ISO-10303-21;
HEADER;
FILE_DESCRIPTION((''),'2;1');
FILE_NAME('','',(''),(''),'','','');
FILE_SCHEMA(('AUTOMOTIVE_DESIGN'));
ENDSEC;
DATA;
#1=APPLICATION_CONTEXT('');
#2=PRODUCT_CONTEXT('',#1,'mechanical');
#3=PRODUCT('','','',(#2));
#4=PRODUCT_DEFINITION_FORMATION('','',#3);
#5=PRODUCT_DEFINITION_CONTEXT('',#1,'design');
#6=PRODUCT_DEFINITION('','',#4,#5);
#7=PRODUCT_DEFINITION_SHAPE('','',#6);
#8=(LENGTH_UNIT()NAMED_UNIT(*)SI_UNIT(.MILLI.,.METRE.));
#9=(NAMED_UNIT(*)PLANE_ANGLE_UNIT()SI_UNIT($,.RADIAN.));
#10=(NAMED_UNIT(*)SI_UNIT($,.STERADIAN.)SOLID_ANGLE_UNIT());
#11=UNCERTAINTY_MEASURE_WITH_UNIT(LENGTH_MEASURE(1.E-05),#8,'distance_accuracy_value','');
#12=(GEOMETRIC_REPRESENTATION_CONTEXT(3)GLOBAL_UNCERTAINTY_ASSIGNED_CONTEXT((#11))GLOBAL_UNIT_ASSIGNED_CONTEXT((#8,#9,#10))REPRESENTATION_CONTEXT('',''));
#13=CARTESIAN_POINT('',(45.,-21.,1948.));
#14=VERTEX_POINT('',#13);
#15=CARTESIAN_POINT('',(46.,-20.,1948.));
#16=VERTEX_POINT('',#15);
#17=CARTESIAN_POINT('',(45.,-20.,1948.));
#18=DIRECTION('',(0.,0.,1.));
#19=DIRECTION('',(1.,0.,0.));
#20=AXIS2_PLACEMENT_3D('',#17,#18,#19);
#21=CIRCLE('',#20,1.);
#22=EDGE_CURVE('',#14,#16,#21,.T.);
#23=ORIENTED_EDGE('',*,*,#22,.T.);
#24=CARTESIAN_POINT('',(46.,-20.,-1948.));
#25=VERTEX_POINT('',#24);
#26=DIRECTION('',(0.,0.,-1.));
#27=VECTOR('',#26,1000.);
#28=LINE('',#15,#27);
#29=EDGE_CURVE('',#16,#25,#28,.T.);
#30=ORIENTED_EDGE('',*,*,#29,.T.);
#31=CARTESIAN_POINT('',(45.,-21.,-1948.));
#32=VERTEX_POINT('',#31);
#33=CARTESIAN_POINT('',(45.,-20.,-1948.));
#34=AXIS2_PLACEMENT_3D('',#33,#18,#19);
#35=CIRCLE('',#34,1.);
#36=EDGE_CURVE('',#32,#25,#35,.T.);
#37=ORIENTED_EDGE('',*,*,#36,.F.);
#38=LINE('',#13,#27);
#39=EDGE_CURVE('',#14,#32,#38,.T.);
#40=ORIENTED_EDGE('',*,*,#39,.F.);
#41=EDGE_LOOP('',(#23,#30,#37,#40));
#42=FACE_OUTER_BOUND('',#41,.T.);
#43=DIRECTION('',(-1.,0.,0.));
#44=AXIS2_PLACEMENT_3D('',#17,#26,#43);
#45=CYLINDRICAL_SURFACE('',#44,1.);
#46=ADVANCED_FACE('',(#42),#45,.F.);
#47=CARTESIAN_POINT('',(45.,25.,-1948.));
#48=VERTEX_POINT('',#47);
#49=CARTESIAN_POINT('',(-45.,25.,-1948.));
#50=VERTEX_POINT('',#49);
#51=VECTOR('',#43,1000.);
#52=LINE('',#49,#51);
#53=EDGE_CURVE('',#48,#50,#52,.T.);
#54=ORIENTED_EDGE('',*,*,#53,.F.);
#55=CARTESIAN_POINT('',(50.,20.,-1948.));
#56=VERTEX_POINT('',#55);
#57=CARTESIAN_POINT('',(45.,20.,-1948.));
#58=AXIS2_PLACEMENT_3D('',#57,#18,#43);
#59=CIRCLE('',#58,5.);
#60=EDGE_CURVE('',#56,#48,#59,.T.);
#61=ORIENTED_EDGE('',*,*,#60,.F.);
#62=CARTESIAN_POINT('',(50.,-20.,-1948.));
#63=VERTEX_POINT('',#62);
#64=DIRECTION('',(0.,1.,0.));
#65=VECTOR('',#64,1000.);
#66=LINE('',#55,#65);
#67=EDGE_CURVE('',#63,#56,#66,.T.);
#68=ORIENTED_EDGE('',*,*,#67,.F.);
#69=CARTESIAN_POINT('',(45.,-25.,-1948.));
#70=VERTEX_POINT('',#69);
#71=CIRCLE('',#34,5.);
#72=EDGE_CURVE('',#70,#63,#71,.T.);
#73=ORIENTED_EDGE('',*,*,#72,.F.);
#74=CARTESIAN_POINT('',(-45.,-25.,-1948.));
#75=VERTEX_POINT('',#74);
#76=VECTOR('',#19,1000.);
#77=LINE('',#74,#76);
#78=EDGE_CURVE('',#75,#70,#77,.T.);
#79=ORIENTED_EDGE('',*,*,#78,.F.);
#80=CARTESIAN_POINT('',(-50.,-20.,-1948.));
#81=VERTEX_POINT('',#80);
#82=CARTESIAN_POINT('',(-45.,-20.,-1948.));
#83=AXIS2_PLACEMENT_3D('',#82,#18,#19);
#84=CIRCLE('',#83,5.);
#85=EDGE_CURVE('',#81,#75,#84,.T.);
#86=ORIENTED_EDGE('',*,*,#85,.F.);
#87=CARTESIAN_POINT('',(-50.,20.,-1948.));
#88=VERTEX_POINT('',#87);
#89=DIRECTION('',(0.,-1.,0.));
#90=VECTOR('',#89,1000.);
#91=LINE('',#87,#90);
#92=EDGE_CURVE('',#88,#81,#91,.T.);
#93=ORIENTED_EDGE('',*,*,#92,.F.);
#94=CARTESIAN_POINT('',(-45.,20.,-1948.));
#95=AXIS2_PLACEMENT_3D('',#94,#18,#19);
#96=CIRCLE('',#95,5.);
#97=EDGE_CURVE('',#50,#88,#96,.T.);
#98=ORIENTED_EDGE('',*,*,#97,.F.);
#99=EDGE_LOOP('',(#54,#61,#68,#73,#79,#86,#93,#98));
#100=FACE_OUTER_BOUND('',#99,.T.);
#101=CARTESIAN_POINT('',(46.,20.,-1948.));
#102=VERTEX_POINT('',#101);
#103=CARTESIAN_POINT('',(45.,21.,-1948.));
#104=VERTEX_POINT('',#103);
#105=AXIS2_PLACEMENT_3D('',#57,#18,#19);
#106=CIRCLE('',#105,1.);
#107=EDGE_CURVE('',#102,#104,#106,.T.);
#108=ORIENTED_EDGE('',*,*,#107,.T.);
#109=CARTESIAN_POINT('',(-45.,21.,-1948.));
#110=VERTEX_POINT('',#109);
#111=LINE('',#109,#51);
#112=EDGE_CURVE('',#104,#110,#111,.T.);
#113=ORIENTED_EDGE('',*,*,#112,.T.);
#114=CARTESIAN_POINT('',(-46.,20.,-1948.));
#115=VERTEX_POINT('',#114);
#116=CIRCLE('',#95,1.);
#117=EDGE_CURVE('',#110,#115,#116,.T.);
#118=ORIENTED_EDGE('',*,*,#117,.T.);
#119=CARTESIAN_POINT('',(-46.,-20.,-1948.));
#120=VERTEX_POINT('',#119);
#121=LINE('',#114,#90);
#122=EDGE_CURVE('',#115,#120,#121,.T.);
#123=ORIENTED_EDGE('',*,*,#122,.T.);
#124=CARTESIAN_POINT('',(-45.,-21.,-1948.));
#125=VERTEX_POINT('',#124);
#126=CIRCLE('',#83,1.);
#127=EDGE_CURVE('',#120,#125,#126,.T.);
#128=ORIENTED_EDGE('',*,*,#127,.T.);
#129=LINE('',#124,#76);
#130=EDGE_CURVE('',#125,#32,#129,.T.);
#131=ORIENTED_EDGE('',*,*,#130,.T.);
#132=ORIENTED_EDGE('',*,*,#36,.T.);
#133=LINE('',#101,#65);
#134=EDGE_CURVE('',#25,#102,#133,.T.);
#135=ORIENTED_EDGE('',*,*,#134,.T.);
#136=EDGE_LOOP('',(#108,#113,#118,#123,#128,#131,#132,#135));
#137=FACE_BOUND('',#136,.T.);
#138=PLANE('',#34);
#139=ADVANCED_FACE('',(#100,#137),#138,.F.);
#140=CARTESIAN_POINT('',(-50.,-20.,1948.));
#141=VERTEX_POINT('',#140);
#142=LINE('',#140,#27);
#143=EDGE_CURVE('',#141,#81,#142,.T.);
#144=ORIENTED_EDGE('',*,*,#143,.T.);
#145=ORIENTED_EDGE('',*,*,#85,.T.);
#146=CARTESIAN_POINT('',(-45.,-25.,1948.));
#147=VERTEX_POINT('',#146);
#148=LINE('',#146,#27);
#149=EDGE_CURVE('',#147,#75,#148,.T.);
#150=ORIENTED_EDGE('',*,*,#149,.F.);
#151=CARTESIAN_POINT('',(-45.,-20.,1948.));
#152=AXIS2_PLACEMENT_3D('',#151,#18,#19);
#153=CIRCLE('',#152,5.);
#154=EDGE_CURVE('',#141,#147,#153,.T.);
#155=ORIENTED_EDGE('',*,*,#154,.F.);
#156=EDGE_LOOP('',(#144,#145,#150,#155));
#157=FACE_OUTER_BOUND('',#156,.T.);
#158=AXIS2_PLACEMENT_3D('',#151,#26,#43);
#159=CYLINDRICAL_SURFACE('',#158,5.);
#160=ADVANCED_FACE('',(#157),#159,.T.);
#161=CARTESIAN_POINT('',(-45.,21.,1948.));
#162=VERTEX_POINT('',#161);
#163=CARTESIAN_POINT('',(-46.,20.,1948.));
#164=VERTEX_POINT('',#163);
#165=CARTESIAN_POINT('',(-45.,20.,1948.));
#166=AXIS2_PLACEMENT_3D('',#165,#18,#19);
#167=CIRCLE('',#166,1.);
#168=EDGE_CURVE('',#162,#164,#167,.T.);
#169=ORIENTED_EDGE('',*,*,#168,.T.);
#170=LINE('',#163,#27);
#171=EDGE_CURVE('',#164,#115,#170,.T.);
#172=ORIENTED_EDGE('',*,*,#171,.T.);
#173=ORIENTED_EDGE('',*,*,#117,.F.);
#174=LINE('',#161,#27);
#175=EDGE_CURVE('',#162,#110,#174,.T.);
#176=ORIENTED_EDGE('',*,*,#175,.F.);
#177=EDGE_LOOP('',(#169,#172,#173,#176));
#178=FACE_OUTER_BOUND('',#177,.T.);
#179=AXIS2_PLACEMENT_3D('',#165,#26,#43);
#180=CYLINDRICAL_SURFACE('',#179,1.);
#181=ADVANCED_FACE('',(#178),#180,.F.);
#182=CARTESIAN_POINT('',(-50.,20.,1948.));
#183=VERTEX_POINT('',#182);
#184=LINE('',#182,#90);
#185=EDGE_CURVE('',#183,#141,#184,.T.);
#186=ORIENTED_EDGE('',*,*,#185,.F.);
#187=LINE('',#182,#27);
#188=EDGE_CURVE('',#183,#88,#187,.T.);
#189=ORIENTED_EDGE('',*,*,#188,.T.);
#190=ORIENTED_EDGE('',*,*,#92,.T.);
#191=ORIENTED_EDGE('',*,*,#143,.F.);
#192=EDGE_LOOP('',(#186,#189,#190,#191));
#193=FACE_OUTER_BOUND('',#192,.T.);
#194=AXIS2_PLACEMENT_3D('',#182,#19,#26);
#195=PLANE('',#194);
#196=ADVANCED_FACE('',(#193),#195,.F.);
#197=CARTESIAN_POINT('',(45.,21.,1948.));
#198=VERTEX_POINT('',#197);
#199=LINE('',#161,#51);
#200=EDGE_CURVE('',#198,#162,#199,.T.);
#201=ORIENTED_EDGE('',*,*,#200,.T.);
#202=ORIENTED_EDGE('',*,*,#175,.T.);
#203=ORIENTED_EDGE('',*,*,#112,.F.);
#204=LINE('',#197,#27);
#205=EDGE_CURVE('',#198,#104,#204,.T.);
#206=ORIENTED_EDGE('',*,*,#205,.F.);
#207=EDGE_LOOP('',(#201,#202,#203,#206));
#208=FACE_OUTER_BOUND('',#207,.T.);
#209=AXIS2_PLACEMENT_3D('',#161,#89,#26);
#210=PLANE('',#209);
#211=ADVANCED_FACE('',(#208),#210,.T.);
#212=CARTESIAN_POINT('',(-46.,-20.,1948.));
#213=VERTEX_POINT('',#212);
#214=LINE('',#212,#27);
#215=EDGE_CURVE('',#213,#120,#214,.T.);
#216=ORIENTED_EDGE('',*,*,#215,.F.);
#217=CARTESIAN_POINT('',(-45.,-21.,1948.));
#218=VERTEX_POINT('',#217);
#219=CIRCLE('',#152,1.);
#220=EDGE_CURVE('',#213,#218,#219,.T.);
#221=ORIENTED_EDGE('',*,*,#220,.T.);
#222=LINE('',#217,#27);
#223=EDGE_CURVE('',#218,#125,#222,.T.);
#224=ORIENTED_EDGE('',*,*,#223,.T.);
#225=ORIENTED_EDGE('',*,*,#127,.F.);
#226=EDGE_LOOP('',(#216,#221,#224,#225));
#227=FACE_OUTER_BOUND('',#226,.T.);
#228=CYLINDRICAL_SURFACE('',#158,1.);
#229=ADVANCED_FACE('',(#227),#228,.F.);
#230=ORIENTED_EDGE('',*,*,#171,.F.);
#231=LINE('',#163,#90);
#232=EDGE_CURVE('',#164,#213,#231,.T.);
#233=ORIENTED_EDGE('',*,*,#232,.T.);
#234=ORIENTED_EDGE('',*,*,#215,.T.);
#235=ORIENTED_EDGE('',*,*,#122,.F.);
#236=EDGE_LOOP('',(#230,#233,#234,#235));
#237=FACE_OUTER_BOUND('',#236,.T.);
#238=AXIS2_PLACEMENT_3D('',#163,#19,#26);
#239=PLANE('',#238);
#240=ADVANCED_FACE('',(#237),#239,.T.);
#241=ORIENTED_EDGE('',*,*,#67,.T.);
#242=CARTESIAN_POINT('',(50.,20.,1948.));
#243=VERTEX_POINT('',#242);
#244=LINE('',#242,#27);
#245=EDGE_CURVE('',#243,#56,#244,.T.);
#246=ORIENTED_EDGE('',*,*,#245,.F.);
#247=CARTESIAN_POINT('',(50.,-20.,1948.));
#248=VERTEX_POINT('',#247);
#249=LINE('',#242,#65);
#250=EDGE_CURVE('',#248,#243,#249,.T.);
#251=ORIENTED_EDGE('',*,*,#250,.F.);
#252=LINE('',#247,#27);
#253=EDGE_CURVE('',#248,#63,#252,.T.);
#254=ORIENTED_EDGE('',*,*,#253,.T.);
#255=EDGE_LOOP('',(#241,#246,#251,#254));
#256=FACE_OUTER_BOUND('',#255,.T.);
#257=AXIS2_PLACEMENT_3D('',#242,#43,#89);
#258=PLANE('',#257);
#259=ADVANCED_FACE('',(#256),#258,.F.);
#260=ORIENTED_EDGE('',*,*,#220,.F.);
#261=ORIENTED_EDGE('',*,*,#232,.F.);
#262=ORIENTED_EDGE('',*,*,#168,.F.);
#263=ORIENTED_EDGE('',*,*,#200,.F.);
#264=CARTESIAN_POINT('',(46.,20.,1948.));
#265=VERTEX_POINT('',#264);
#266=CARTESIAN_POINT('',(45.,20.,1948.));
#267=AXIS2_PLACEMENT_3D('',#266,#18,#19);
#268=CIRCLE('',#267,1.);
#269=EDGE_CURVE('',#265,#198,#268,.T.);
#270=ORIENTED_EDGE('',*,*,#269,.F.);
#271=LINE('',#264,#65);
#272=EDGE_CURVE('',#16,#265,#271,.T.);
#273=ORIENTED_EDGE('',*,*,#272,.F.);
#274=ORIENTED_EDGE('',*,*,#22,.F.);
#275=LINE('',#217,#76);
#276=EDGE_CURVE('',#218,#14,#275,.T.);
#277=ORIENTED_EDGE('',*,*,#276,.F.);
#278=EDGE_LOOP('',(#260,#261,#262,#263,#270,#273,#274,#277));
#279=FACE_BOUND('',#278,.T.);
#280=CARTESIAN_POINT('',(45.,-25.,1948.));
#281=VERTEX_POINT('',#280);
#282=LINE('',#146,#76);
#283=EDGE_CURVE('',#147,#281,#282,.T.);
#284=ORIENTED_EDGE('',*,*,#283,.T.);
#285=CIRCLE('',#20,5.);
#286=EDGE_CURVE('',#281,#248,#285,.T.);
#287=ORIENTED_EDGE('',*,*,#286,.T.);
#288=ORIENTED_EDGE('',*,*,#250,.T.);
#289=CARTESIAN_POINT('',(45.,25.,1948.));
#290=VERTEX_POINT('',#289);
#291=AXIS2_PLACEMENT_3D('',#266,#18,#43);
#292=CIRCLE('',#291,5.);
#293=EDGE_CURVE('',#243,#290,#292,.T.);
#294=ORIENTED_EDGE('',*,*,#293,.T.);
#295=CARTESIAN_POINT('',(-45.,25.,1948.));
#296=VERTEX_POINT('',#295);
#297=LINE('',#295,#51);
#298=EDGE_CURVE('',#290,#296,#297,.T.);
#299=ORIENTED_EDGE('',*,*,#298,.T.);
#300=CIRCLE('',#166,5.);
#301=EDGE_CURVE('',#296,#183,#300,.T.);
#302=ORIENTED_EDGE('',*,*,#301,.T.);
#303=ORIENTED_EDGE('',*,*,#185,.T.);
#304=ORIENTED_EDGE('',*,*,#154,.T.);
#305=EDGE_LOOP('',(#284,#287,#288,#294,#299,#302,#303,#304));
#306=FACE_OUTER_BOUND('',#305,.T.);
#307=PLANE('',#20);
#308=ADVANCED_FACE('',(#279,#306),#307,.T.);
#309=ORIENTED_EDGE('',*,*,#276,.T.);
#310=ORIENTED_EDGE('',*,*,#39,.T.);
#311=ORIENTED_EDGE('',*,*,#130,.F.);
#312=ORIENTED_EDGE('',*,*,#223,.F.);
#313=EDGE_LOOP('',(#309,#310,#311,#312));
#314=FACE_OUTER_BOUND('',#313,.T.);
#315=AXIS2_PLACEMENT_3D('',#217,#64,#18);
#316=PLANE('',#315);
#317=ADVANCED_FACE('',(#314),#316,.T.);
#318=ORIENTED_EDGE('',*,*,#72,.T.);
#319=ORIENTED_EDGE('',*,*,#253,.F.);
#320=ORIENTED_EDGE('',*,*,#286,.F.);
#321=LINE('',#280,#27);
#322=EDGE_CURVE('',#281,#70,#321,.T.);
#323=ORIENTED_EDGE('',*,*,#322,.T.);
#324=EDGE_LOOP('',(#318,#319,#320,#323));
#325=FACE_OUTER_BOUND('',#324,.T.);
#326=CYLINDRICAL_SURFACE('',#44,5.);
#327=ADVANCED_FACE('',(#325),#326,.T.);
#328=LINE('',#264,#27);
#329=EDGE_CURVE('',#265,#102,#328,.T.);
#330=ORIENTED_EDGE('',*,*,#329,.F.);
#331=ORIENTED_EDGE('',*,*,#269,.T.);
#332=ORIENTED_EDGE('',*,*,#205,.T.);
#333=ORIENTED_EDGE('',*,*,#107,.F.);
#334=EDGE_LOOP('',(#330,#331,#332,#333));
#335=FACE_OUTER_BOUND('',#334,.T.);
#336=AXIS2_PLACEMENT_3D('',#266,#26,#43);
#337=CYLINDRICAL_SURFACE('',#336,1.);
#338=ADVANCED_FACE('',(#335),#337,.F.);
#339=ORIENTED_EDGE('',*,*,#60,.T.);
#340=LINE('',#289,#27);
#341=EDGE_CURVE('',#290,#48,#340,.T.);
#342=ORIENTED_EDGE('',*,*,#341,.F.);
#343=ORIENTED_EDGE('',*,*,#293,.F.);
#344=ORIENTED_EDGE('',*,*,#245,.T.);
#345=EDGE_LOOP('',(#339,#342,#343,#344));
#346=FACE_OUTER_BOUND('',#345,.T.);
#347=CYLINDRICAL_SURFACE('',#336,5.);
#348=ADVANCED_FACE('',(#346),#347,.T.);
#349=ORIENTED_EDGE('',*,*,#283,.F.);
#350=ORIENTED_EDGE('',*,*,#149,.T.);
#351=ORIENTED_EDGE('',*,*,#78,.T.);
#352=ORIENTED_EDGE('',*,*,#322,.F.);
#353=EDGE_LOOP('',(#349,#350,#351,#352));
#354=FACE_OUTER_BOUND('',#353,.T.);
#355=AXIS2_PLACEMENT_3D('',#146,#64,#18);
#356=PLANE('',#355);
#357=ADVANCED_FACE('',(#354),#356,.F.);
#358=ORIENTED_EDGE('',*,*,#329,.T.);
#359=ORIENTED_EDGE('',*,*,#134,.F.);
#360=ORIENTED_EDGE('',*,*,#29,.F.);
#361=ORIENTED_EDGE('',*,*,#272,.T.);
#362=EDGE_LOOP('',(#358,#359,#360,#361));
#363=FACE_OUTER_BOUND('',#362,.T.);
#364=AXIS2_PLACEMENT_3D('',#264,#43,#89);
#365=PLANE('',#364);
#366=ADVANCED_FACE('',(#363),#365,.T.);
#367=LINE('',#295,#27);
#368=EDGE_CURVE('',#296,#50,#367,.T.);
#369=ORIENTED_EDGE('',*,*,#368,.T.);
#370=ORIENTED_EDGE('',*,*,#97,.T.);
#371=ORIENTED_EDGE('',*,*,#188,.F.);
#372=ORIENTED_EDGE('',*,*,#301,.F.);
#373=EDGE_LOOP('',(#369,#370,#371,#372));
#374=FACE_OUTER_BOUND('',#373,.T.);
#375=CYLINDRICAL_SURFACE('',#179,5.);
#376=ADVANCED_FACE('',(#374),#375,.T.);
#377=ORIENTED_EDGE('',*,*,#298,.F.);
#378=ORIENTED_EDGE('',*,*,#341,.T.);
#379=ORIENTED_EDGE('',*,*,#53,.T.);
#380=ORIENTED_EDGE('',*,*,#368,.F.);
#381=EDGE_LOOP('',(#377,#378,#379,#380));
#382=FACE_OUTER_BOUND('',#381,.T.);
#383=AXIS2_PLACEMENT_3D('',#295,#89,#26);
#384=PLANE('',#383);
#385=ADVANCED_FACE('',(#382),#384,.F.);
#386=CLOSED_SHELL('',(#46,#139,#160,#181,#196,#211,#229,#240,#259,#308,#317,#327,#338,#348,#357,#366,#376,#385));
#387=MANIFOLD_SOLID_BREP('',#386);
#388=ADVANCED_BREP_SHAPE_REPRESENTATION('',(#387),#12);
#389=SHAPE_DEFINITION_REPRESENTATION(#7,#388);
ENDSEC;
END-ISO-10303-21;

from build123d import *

# Parameters (mm, degrees)
EXTRUDE_1_DEPTH = 1948


with BuildPart() as part:
    # 草图1 → 拉伸-薄壁1 (new, symmetric)
    with BuildSketch(Plane.XY):
        with BuildLine():
            Line((-45, 25), (45, 25))
            ThreePointArc((45, 25), (48.535533906, 23.535533906), (50, 20))
            Line((50, 20), (50, -20))
            ThreePointArc((50, -20), (48.535533906, -23.535533906), (45, -25))
            Line((45, -25), (-45, -25))
            ThreePointArc((-45, -25), (-48.535533906, -23.535533906), (-50, -20))
            Line((-50, -20), (-50, 20))
            ThreePointArc((-50, 20), (-48.535533906, 23.535533906), (-45, 25))
        make_face()
        with BuildLine():
            Line((-45, 21), (45, 21))
            ThreePointArc((45, 21), (45.707106781, 20.707106781), (46, 20))
            Line((46, 20), (46, -20))
            ThreePointArc((46, -20), (45.707106781, -20.707106781), (45, -21))
            Line((45, -21), (-45, -21))
            ThreePointArc((-45, -21), (-45.707106781, -20.707106781), (-46, -20))
            Line((-46, -20), (-46, 20))
            ThreePointArc((-46, 20), (-45.707106781, 20.707106781), (-45, 21))
        make_face(mode=Mode.SUBTRACT)
    extrude(amount=EXTRUDE_1_DEPTH, both=True)


solid = part.part
